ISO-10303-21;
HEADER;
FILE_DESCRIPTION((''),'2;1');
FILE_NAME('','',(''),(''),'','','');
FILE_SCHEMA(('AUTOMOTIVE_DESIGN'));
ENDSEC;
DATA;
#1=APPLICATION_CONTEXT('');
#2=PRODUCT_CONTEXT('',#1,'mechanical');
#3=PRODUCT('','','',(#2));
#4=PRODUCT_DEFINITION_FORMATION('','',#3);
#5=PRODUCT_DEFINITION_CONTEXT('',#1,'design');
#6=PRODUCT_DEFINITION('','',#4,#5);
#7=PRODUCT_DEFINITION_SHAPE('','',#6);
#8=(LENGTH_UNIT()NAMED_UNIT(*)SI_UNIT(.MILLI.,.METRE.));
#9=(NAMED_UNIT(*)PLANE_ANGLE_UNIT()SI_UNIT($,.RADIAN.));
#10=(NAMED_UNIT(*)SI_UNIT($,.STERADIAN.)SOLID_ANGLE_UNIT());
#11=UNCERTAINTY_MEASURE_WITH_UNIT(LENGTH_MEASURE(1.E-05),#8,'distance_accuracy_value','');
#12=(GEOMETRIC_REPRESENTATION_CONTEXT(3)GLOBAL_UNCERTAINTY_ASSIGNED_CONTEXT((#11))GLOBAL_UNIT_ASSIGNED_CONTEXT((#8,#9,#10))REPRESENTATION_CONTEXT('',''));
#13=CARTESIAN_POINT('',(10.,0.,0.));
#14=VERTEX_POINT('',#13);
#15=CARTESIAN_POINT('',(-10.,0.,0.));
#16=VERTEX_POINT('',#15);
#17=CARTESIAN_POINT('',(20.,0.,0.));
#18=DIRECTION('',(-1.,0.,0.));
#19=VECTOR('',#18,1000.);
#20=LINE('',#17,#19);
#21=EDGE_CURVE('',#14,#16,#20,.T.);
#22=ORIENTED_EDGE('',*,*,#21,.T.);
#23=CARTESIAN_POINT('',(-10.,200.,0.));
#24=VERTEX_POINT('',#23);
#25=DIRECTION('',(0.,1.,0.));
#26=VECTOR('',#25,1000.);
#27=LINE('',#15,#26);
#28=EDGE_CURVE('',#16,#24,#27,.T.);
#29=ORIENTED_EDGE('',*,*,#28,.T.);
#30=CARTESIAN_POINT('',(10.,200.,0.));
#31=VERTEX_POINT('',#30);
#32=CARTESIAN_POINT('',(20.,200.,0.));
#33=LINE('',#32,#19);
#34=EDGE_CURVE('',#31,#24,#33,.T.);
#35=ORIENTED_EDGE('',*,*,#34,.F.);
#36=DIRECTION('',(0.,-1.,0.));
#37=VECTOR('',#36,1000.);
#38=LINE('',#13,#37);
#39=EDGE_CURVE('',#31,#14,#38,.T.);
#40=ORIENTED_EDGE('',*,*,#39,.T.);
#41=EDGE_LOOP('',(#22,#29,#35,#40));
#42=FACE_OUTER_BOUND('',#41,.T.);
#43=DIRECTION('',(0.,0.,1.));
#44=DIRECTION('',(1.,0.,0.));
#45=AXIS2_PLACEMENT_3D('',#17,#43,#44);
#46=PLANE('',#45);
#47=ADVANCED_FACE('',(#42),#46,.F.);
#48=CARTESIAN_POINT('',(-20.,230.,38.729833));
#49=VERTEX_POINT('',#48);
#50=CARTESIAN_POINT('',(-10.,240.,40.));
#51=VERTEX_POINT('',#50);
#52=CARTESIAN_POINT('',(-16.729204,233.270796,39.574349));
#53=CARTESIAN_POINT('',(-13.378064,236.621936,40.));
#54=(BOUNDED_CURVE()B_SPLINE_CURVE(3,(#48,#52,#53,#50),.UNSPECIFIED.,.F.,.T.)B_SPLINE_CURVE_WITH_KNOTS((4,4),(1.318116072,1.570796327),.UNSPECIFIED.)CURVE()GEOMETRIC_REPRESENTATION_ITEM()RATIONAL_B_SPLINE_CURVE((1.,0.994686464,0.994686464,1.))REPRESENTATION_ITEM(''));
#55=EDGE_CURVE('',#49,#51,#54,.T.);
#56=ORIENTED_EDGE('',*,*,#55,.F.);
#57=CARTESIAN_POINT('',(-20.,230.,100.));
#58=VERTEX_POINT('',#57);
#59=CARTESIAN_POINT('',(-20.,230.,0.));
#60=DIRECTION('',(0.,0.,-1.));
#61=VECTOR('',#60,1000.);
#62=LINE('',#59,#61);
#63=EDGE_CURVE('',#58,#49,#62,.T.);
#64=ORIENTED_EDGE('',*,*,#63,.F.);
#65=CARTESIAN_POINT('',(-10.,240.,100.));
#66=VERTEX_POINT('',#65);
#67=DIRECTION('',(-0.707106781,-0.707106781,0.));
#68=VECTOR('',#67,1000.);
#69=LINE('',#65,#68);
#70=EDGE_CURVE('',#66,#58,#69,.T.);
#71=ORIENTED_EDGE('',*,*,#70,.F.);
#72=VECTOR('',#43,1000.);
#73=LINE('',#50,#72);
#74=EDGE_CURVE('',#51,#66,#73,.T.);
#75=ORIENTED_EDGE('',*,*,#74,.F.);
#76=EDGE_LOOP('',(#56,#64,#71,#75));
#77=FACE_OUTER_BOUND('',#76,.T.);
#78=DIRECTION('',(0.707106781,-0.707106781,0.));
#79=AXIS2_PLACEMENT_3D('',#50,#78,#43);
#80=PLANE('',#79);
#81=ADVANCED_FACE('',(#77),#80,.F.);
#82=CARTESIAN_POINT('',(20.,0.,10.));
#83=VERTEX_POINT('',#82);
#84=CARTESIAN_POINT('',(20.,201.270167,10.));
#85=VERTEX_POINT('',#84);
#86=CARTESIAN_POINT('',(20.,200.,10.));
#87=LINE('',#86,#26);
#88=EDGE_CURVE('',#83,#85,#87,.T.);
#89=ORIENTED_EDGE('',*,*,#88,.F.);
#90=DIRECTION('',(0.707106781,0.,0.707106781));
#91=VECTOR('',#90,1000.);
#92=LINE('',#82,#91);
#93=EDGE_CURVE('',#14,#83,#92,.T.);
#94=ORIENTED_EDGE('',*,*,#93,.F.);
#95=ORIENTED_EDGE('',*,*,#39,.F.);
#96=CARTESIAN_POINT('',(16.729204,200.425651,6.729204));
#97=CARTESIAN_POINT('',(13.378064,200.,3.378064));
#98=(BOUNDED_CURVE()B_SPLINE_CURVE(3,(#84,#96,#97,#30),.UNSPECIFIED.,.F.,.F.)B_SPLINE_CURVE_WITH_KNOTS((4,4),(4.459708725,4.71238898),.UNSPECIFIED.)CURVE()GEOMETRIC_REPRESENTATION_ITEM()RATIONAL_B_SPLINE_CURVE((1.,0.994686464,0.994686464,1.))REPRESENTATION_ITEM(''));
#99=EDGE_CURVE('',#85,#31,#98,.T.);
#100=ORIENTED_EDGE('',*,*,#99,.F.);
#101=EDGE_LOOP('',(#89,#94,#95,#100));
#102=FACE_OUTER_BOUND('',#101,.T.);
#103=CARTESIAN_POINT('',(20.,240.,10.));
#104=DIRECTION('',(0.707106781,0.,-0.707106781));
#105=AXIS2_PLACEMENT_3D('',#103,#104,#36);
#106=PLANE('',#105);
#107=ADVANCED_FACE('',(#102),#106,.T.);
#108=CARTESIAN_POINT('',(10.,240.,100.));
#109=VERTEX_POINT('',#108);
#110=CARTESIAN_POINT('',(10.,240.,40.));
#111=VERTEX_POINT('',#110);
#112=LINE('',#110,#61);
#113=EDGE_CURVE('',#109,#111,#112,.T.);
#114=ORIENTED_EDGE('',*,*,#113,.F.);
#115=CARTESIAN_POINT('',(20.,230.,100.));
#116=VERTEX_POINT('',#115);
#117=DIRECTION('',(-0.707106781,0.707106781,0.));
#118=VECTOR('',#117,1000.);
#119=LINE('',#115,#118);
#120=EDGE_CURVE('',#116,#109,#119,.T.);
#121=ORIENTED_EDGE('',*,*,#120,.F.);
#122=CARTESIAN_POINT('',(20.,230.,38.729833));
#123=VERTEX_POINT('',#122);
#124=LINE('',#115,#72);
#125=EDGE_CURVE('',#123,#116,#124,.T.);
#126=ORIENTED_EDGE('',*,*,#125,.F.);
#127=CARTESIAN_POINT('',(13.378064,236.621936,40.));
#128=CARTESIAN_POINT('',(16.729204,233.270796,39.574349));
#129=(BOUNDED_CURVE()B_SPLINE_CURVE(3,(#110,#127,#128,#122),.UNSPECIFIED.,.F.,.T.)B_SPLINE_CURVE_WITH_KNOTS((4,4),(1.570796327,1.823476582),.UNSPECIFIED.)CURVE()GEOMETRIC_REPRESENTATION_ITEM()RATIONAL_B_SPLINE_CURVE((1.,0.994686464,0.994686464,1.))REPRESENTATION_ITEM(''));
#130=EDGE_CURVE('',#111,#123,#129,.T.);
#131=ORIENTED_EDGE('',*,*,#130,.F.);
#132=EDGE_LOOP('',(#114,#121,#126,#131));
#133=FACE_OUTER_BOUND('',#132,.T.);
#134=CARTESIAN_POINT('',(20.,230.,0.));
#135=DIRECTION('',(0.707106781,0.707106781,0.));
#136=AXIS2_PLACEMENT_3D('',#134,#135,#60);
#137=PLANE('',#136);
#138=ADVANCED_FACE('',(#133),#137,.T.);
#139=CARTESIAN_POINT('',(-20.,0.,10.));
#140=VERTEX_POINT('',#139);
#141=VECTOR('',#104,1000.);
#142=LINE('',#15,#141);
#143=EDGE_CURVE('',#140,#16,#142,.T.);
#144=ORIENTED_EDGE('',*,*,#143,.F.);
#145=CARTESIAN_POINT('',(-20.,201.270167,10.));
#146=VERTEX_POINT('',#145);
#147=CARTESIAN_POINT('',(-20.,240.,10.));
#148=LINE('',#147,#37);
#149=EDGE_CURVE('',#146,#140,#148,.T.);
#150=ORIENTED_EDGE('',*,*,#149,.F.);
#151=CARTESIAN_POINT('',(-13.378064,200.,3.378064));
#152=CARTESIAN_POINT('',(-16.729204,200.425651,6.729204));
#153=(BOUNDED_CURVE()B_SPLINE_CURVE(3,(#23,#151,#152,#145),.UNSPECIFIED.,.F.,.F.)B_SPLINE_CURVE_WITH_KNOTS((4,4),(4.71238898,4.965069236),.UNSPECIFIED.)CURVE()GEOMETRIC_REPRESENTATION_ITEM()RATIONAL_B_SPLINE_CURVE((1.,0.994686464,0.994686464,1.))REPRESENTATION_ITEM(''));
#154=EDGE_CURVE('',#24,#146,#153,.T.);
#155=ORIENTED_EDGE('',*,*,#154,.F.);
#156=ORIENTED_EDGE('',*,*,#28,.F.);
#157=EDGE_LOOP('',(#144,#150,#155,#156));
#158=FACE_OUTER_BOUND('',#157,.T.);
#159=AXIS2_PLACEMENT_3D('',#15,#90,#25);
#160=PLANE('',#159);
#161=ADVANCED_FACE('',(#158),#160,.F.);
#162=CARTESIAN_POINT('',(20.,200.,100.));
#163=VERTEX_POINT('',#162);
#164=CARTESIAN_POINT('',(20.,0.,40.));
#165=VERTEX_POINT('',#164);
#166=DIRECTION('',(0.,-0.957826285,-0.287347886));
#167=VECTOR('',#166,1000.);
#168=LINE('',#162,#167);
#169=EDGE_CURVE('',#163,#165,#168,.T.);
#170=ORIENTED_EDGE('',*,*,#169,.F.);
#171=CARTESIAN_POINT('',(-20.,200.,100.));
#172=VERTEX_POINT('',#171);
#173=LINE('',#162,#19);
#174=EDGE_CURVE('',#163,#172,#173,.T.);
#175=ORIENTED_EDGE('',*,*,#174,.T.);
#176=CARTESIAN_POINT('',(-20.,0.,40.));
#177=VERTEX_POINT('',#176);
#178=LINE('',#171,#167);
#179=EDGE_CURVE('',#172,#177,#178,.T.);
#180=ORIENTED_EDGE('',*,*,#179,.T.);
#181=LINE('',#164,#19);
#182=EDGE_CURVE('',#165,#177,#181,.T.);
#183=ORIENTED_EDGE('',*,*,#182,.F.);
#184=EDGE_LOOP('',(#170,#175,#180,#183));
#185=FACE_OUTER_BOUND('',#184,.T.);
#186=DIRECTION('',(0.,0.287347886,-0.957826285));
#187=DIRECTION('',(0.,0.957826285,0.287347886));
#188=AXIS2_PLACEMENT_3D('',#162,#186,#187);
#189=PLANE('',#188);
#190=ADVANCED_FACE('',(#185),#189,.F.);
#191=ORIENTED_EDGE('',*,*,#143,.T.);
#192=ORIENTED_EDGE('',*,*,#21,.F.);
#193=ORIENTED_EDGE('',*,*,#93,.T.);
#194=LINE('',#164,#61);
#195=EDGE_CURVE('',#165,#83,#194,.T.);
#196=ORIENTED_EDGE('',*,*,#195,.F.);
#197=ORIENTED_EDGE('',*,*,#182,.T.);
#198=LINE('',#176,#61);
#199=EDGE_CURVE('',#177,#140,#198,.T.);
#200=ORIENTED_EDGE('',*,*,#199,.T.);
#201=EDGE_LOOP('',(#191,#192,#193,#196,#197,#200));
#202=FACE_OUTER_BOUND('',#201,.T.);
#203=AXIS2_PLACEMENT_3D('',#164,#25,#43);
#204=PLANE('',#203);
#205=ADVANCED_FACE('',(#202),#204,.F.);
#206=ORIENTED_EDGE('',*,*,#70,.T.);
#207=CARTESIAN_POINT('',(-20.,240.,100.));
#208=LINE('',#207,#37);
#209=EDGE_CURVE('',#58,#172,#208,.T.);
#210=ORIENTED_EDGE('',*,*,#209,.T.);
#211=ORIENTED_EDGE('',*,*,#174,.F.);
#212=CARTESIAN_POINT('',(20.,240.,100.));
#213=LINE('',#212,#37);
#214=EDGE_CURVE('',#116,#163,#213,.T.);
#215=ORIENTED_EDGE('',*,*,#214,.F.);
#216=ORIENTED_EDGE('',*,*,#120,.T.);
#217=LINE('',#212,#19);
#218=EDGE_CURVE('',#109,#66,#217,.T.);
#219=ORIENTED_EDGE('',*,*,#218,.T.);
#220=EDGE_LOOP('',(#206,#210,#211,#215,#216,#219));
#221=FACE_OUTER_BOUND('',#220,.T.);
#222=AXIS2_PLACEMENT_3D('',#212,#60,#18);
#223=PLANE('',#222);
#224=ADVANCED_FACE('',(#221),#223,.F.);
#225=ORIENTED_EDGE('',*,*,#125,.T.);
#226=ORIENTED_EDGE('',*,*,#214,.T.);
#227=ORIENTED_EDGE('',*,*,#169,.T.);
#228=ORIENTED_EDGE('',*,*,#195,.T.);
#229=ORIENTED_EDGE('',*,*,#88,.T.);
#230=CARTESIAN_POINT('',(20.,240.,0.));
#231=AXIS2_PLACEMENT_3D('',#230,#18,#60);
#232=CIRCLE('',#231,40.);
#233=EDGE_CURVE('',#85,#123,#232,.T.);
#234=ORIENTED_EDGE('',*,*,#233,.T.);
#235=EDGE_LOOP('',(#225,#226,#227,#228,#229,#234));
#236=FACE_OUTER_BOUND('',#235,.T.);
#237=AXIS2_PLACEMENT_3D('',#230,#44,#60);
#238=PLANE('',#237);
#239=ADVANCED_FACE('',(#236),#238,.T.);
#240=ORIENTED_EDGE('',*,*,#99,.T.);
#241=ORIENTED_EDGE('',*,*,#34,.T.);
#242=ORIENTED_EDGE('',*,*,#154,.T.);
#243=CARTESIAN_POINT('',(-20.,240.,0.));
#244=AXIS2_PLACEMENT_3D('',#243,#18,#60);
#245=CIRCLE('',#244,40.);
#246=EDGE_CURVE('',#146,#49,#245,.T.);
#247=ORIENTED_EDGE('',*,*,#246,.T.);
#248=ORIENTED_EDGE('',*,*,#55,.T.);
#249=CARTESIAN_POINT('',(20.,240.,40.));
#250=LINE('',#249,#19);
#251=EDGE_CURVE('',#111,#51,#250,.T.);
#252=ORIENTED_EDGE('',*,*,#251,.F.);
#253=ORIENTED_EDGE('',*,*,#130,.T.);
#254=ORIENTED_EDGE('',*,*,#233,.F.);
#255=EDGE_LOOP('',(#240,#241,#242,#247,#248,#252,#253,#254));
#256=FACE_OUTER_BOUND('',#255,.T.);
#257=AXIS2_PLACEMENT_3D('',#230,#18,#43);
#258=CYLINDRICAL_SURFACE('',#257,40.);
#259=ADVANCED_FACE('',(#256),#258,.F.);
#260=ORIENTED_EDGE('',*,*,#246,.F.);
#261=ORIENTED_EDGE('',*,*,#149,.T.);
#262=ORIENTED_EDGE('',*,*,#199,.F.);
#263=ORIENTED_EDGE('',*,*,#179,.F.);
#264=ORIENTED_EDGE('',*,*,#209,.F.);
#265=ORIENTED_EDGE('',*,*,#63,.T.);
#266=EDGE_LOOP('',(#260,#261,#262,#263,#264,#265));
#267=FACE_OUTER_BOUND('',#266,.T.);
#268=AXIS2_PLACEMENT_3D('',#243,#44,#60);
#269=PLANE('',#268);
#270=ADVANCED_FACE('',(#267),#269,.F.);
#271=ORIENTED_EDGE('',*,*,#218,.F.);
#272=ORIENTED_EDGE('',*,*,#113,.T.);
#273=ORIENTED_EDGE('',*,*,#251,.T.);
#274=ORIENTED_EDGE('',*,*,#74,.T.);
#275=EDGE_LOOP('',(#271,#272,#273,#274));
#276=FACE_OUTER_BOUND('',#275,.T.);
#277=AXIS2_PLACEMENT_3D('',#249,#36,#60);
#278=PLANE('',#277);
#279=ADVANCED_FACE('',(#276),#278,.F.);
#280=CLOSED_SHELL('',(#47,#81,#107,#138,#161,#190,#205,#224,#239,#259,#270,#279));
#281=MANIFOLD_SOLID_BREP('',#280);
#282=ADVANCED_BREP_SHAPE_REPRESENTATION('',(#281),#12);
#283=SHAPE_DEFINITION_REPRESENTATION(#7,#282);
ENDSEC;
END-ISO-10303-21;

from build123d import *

# Parameters (mm, degrees)
BOSS_EXTRUDE1_DEPTH = 20
CHAMFER1_SIZE       = 10


with BuildPart() as part:
    # Sketch1 → Boss-Extrude1 (new, symmetric)
    with BuildSketch(Plane(origin=(0, 0, 0), x_dir=(0, 0, -1), z_dir=(1, 0, 0))):
        with BuildLine():
            Line((0, 0), (0, 200))
            ThreePointArc((0, 200), (-28.284271247, 211.715728753), (-40, 240))
            Line((-40, 240), (-100, 240))
            Line((-100, 240), (-100, 200))
            Line((-100, 200), (-40, 0))
            Line((-40, 0), (0, 0))
        make_face()
    extrude(amount=BOSS_EXTRUDE1_DEPTH, both=True)

    # Chamfer1
    chamfer1_edges = [part.edges().sort_by_distance(p)[0] for p in [
        (20, 240, 70),
        (-20, 240, 70),
        (20, 100, 0),
        (-20, 100, 0),
    ]]
    chamfer(chamfer1_edges, length=CHAMFER1_SIZE)


solid = part.part
